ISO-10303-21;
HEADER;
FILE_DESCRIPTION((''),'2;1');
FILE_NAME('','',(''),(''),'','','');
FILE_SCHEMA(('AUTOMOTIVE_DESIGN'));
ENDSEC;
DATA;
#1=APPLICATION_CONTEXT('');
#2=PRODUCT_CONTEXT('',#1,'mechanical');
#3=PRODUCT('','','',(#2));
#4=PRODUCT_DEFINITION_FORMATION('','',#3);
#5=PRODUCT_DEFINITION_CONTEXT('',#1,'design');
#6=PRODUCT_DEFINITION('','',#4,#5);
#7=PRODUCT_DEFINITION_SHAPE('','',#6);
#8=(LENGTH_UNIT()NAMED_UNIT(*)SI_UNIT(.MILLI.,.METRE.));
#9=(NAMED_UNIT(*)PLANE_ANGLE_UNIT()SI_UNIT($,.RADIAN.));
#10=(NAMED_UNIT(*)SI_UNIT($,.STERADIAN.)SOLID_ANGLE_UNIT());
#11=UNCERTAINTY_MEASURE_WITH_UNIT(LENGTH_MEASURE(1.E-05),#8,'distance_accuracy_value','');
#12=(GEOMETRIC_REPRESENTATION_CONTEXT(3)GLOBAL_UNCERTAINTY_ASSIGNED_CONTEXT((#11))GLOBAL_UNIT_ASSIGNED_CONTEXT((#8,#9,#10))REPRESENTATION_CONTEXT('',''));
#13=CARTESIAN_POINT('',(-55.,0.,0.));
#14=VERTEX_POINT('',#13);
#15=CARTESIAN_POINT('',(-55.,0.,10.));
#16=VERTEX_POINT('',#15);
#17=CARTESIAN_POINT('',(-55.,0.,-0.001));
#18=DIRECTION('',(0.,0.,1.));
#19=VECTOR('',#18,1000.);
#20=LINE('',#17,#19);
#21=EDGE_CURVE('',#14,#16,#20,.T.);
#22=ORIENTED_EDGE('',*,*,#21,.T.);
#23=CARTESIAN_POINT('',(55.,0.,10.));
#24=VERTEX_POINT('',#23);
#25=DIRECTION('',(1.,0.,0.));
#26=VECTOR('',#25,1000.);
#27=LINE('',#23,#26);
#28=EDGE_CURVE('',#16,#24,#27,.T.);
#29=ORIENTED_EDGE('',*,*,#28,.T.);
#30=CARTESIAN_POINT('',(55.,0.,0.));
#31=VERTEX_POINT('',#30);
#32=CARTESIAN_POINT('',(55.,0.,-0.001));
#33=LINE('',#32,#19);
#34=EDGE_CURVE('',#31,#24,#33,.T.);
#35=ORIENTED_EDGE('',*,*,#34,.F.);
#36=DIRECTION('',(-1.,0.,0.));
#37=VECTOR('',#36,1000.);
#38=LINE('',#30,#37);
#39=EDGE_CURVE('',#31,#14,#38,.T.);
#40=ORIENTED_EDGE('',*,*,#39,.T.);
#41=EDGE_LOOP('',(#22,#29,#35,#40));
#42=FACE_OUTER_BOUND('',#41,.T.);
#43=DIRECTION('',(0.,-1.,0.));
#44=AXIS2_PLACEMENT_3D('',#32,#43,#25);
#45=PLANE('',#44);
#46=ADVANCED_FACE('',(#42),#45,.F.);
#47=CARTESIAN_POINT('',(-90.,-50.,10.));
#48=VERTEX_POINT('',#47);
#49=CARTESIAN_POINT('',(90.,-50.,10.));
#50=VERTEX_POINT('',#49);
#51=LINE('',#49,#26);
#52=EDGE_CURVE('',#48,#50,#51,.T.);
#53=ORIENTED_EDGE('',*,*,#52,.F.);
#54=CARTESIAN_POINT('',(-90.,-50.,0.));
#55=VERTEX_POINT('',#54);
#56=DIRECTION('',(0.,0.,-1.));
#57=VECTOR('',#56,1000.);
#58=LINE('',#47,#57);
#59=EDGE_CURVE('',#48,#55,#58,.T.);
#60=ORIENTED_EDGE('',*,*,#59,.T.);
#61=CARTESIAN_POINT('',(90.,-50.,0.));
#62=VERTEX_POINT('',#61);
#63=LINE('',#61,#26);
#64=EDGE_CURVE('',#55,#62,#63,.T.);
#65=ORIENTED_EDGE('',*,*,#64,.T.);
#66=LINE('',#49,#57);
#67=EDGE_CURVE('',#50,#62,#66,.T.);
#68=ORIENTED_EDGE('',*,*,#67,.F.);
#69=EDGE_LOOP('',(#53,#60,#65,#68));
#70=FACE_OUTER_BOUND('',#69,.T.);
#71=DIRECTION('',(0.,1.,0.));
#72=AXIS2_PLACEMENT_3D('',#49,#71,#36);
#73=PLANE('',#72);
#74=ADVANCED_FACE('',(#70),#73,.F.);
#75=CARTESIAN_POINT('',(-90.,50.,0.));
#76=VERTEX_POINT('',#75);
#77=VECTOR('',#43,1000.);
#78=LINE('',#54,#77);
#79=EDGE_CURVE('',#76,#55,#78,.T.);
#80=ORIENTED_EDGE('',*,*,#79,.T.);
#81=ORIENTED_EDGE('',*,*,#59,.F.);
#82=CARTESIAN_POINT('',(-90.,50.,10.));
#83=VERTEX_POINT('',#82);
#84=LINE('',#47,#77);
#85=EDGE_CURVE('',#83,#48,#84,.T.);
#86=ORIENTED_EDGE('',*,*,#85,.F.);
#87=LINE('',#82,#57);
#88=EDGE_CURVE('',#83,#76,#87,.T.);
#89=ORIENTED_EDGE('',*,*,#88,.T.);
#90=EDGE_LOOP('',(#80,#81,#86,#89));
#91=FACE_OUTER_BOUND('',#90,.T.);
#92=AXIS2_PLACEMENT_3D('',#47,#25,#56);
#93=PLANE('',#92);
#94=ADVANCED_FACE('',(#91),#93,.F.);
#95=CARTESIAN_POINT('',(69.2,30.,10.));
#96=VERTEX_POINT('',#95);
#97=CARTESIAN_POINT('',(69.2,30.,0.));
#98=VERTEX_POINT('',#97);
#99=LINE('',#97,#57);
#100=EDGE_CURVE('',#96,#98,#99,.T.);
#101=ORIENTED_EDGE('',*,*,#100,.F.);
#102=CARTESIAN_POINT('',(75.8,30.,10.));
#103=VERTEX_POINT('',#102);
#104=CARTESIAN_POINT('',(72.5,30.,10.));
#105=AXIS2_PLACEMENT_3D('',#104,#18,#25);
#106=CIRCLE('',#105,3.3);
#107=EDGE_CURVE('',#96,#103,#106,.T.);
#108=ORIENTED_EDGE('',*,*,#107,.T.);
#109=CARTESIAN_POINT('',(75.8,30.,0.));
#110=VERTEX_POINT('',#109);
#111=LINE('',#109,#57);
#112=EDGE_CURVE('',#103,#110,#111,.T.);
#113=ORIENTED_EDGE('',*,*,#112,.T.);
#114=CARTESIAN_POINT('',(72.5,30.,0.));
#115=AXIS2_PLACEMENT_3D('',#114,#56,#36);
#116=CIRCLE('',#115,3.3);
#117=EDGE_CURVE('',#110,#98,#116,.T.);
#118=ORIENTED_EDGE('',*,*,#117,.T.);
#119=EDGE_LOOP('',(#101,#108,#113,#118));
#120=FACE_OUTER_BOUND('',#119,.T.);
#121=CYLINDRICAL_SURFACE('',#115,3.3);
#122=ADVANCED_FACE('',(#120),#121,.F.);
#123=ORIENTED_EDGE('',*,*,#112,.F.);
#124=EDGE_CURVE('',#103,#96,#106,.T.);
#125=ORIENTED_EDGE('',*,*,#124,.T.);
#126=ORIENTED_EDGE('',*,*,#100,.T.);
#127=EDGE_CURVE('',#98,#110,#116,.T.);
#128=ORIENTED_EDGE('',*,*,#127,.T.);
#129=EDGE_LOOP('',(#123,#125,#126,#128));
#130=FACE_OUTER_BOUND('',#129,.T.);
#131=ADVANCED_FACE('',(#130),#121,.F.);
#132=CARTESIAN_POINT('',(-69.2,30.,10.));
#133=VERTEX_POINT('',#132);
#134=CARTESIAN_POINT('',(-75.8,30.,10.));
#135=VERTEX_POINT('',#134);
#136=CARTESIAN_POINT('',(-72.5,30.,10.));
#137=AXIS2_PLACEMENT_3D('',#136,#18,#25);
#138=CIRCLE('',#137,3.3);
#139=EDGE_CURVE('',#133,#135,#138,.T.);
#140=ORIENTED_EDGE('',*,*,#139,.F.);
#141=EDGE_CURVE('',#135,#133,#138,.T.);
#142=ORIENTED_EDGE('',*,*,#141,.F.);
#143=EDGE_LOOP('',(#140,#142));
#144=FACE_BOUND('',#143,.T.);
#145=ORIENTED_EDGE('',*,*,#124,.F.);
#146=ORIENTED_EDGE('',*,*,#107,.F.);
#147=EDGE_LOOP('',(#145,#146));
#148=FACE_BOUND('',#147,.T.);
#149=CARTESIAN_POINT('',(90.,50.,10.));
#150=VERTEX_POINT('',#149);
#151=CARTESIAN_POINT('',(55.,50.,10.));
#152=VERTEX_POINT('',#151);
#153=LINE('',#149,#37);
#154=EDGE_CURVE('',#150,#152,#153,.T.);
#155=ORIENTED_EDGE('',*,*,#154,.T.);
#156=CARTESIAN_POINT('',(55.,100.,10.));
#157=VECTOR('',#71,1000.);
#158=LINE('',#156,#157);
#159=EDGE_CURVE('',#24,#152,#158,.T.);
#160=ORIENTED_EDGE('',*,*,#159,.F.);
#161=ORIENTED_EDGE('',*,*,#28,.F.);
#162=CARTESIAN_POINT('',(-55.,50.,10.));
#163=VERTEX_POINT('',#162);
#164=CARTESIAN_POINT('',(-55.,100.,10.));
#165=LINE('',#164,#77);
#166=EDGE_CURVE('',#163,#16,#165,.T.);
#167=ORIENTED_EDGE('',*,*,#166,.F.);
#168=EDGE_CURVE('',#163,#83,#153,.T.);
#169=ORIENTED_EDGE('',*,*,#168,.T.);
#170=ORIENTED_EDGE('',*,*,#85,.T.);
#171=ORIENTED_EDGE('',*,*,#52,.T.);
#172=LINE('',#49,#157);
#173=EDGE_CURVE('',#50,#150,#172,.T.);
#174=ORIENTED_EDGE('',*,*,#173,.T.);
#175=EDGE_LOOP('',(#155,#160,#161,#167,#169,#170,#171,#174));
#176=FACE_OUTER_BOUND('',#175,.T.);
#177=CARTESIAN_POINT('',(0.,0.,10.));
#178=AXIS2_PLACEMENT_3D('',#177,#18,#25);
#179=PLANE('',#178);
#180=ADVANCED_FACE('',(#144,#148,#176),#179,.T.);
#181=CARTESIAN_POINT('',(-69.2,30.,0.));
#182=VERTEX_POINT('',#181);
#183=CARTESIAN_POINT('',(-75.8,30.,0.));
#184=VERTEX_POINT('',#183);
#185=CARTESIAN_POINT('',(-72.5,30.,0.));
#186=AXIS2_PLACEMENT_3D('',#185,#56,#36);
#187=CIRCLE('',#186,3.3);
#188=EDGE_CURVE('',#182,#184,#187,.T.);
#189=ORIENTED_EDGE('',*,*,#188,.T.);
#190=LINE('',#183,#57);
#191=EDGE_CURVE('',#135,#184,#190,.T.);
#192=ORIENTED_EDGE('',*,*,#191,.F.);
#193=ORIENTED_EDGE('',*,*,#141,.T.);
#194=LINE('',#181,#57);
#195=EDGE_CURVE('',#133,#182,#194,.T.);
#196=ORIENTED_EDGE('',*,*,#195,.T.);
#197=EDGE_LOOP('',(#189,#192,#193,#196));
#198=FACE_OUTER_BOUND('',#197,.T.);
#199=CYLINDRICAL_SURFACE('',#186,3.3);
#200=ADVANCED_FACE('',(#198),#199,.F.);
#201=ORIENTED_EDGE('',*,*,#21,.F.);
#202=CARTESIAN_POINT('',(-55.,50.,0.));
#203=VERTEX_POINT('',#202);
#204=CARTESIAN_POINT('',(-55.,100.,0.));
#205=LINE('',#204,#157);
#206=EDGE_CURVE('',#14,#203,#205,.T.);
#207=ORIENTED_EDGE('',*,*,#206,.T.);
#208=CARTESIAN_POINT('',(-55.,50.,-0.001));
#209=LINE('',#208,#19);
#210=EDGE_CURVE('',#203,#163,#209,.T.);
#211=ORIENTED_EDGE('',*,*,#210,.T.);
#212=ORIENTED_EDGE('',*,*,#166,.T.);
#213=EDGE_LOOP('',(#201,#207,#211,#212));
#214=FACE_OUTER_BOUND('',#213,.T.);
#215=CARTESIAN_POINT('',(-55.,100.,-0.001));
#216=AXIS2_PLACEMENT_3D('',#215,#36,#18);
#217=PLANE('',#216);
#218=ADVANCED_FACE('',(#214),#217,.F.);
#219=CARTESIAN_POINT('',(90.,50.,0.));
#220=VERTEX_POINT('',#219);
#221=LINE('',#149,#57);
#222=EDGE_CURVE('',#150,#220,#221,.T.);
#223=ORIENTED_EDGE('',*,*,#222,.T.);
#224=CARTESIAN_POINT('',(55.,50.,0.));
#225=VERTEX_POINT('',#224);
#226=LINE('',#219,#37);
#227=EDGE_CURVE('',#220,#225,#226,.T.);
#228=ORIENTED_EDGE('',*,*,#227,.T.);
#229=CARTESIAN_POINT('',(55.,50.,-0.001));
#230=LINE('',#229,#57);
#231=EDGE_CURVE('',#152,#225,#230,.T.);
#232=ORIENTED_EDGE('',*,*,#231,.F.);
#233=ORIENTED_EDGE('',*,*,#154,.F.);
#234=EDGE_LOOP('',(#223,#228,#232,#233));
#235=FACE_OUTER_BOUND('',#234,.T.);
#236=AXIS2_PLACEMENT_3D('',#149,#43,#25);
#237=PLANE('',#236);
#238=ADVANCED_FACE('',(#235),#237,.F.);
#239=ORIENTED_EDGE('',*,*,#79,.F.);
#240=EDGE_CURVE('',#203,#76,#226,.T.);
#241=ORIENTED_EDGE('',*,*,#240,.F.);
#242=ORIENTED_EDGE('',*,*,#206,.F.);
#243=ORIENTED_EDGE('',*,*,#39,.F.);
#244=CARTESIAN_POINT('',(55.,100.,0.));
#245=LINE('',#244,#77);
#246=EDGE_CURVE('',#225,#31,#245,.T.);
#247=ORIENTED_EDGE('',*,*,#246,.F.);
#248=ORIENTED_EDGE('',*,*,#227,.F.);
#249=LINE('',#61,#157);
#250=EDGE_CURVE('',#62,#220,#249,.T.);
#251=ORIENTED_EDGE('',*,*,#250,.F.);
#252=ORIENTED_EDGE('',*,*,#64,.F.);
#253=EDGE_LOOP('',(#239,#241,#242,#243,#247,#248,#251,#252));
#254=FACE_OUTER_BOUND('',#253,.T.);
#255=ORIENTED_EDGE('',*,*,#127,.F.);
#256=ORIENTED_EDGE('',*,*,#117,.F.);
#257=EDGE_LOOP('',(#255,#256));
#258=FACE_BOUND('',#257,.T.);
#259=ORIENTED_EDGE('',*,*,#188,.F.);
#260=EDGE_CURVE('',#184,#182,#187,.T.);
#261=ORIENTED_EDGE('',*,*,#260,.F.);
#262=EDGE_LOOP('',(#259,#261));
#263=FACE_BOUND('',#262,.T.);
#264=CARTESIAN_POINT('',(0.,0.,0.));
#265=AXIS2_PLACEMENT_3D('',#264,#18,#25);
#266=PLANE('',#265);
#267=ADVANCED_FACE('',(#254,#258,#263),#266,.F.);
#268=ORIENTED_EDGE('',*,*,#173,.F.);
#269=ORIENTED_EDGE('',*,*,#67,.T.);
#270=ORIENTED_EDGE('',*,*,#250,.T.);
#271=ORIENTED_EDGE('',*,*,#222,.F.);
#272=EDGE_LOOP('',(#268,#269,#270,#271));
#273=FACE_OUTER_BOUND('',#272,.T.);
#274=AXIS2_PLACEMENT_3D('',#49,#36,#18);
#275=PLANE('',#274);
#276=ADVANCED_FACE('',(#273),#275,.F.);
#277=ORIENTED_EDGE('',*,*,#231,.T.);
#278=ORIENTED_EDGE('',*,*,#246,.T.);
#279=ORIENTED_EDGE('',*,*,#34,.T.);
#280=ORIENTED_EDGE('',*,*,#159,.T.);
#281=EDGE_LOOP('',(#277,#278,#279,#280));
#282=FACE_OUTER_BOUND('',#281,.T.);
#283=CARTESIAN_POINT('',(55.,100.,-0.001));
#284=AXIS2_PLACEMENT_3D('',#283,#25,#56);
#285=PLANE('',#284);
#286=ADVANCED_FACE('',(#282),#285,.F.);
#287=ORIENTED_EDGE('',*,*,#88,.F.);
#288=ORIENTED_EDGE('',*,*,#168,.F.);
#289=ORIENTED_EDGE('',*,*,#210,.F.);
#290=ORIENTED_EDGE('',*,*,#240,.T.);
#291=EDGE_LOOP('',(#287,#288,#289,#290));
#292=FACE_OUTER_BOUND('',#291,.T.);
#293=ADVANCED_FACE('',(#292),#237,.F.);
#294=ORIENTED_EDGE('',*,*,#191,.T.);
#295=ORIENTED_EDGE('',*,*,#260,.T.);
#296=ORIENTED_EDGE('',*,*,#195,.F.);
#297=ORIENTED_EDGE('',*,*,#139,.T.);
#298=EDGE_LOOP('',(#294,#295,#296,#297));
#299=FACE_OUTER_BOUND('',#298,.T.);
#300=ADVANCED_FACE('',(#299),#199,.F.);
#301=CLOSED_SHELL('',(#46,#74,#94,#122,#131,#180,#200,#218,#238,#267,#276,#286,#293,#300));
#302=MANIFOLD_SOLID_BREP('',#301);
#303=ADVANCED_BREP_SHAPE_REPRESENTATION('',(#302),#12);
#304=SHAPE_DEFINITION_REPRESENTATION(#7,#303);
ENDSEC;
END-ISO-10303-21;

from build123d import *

# Parameters (mm, degrees)
SKETCH_1_W          = 180
SKETCH_1_H          = 100
EXTRUDE_1_DEPTH     = 10
CUT_EXTRUDE_1_REACH = 105.441
SKETCH_2_W          = 110
SKETCH_2_H          = 100
HOLE_WIZARD_M6_1_D  = 6.6


with BuildPart() as part:
    # 草图1 → 凸台-拉伸1 (new body)
    with BuildSketch(Plane.XY):
        Rectangle(SKETCH_1_W, SKETCH_1_H)
    extrude(amount=EXTRUDE_1_DEPTH)

    # 草图2 → 切除-拉伸1 (cut, up to next)
    with BuildSketch(Plane.XY.offset(10), mode=Mode.PRIVATE) as cut_extrude_1_sk1:
        with Locations((0, 50)):
            Rectangle(SKETCH_2_W, SKETCH_2_H)
    cut_extrude_1_tool1 = extrude(cut_extrude_1_sk1.sketch, amount=-CUT_EXTRUDE_1_REACH, mode=Mode.PRIVATE) & part.part
    add(cut_extrude_1_tool1.solids().sort_by_distance((0, 50, 10))[0], mode=Mode.SUBTRACT)

    # M6 间隙孔1 (through all)
    with Locations(Plane(origin=(0, 0, 0), x_dir=(-1, 0, 0), z_dir=(0, 0, -1))):
        with Locations((-72.5, 30), (72.5, 30)):
            Hole(HOLE_WIZARD_M6_1_D / 2)


solid = part.part
